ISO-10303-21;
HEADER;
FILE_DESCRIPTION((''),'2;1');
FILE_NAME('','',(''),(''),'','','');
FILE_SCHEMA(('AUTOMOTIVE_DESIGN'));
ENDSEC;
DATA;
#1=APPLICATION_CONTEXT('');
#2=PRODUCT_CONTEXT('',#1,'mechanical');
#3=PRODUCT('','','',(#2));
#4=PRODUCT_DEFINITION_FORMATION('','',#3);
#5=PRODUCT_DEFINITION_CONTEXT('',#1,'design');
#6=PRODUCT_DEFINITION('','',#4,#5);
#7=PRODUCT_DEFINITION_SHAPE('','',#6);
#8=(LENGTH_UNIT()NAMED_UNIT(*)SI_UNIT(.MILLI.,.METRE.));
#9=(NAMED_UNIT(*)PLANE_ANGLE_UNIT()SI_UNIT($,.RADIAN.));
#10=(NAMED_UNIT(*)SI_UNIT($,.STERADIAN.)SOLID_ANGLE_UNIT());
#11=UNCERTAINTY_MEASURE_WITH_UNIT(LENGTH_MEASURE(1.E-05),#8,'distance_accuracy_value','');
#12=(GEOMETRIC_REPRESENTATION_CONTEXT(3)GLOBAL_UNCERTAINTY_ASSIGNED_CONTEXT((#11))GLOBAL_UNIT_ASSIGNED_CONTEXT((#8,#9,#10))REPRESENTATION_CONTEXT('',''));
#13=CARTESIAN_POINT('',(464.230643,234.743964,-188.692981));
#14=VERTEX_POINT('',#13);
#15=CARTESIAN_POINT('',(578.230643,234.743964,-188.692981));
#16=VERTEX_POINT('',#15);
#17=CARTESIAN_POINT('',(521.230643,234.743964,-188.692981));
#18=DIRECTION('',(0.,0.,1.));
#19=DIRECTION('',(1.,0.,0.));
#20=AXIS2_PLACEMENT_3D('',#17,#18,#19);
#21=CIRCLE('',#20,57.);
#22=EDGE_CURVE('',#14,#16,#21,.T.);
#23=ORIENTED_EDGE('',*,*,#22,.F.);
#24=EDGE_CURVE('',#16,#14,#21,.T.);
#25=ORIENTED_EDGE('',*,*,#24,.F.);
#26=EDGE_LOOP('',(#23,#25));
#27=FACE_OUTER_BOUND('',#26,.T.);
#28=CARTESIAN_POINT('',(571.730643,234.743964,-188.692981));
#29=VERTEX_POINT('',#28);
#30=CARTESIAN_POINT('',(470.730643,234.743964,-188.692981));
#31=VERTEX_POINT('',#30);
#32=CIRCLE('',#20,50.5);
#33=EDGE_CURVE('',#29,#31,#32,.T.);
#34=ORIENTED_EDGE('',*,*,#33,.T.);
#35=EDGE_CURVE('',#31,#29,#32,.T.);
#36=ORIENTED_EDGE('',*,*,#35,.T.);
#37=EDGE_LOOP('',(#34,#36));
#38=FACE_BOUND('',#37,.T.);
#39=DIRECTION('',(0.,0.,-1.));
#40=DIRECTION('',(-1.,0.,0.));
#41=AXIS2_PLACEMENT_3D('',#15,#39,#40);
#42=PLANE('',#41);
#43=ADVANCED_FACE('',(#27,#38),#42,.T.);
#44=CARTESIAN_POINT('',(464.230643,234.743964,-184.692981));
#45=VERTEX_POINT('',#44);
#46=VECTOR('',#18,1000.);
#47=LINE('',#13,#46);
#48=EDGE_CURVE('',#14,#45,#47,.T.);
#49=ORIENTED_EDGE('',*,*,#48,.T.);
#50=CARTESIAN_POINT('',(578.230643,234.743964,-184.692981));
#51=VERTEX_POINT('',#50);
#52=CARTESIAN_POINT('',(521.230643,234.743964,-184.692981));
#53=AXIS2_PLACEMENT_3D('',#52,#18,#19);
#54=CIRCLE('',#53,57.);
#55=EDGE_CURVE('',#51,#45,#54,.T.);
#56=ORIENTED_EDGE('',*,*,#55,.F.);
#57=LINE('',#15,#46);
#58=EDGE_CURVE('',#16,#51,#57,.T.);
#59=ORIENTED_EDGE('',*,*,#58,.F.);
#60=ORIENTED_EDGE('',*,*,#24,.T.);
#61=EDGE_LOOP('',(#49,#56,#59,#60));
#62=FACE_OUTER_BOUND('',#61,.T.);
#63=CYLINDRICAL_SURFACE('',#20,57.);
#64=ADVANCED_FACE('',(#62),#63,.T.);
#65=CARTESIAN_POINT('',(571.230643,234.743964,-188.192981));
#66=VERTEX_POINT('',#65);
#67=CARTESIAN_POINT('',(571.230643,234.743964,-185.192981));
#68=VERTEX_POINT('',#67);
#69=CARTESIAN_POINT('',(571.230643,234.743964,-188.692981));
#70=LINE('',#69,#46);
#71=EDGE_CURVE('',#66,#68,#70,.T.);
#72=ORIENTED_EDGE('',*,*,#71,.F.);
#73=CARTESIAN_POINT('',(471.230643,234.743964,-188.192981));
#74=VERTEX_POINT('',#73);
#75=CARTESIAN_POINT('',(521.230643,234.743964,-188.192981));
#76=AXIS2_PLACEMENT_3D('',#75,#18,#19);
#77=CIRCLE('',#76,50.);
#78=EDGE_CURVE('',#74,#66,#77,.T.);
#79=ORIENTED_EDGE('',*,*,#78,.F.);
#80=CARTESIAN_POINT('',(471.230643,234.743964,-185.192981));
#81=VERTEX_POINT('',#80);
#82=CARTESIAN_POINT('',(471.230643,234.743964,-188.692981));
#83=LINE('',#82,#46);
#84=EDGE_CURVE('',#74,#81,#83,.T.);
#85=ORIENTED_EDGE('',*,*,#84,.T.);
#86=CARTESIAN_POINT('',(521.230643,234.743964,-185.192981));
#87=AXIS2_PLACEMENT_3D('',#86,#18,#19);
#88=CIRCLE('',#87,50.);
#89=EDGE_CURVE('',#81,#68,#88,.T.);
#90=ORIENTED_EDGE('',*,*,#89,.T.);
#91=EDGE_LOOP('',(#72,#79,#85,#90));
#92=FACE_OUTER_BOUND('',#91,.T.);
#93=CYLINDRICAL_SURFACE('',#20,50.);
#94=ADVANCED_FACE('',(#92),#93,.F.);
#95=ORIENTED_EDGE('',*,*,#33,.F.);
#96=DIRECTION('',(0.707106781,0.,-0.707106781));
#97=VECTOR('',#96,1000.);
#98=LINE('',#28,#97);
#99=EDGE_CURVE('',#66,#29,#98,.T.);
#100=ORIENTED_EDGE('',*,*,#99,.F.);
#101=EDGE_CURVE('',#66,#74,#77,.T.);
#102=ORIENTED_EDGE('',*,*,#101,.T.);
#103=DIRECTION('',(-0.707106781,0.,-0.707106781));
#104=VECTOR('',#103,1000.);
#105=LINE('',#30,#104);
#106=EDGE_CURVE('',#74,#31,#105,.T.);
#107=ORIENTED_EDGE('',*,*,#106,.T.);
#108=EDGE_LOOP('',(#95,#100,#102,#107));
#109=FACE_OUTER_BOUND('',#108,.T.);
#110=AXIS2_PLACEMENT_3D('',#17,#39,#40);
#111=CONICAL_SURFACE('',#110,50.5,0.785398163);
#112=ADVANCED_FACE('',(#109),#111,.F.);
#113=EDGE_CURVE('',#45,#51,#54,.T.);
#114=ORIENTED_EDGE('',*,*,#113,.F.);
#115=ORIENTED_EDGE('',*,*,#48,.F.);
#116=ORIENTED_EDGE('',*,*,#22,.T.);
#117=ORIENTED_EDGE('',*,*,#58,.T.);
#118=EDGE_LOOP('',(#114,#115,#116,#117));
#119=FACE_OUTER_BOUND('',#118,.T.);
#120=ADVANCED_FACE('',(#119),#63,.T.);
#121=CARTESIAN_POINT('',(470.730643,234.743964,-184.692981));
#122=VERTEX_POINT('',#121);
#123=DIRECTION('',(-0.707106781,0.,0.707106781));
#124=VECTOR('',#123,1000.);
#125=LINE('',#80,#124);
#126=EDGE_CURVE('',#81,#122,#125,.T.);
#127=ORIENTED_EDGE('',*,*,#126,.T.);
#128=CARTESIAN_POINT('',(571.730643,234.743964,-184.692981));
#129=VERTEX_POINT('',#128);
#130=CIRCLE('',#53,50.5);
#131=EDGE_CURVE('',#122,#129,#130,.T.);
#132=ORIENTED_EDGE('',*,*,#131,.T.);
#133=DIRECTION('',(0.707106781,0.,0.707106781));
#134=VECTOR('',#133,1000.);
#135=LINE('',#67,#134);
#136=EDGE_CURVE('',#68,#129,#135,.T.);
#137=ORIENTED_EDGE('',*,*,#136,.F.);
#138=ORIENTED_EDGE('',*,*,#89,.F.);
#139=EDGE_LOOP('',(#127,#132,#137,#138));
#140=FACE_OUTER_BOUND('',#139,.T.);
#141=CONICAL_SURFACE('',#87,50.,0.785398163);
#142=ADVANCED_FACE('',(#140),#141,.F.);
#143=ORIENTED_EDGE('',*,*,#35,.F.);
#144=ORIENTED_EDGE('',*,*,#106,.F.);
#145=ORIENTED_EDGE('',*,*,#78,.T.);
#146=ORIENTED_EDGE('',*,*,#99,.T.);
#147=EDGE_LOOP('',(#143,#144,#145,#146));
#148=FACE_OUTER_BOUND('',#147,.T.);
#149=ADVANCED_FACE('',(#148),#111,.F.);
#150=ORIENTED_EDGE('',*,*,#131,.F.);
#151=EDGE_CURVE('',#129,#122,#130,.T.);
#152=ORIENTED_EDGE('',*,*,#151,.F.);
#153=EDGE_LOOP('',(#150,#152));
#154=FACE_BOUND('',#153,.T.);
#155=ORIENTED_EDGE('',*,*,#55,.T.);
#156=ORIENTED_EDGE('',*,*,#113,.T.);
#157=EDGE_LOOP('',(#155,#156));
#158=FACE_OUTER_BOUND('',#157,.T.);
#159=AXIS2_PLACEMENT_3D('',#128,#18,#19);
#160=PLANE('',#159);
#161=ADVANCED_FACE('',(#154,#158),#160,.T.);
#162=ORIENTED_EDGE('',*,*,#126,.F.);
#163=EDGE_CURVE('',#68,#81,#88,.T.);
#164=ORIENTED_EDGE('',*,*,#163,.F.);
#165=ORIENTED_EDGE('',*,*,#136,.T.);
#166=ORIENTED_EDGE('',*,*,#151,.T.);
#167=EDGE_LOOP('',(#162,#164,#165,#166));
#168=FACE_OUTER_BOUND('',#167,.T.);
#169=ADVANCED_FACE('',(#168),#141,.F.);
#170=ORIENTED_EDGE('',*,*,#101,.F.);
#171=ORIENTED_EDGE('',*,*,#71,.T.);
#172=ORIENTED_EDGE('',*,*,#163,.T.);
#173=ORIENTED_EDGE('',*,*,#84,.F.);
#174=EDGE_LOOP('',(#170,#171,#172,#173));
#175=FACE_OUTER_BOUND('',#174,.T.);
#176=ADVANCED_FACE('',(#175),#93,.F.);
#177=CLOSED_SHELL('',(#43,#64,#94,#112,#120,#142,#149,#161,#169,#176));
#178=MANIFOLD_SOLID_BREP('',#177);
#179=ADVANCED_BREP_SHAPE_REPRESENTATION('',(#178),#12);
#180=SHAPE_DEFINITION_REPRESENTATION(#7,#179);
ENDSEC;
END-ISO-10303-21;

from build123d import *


with BuildPart() as part:
    # Sketch1 → Revolve1 (revolve)
    with BuildSketch(Plane(origin=(0, 234.743963655, 0), x_dir=(1, 0, 0), z_dir=(0, 1, 0))):
        Polygon((571.230642584, 185.192981355), (571.730642584, 184.692981355), (578.230642584, 184.692981355), (578.230642584, 188.692981355), (571.730642584, 188.692981355), (571.230642584, 188.192981355), align=None)
    revolve(axis=Axis((521.230642584, 234.743963655, -188.692981355), (0, 0, 1)))


solid = part.part
